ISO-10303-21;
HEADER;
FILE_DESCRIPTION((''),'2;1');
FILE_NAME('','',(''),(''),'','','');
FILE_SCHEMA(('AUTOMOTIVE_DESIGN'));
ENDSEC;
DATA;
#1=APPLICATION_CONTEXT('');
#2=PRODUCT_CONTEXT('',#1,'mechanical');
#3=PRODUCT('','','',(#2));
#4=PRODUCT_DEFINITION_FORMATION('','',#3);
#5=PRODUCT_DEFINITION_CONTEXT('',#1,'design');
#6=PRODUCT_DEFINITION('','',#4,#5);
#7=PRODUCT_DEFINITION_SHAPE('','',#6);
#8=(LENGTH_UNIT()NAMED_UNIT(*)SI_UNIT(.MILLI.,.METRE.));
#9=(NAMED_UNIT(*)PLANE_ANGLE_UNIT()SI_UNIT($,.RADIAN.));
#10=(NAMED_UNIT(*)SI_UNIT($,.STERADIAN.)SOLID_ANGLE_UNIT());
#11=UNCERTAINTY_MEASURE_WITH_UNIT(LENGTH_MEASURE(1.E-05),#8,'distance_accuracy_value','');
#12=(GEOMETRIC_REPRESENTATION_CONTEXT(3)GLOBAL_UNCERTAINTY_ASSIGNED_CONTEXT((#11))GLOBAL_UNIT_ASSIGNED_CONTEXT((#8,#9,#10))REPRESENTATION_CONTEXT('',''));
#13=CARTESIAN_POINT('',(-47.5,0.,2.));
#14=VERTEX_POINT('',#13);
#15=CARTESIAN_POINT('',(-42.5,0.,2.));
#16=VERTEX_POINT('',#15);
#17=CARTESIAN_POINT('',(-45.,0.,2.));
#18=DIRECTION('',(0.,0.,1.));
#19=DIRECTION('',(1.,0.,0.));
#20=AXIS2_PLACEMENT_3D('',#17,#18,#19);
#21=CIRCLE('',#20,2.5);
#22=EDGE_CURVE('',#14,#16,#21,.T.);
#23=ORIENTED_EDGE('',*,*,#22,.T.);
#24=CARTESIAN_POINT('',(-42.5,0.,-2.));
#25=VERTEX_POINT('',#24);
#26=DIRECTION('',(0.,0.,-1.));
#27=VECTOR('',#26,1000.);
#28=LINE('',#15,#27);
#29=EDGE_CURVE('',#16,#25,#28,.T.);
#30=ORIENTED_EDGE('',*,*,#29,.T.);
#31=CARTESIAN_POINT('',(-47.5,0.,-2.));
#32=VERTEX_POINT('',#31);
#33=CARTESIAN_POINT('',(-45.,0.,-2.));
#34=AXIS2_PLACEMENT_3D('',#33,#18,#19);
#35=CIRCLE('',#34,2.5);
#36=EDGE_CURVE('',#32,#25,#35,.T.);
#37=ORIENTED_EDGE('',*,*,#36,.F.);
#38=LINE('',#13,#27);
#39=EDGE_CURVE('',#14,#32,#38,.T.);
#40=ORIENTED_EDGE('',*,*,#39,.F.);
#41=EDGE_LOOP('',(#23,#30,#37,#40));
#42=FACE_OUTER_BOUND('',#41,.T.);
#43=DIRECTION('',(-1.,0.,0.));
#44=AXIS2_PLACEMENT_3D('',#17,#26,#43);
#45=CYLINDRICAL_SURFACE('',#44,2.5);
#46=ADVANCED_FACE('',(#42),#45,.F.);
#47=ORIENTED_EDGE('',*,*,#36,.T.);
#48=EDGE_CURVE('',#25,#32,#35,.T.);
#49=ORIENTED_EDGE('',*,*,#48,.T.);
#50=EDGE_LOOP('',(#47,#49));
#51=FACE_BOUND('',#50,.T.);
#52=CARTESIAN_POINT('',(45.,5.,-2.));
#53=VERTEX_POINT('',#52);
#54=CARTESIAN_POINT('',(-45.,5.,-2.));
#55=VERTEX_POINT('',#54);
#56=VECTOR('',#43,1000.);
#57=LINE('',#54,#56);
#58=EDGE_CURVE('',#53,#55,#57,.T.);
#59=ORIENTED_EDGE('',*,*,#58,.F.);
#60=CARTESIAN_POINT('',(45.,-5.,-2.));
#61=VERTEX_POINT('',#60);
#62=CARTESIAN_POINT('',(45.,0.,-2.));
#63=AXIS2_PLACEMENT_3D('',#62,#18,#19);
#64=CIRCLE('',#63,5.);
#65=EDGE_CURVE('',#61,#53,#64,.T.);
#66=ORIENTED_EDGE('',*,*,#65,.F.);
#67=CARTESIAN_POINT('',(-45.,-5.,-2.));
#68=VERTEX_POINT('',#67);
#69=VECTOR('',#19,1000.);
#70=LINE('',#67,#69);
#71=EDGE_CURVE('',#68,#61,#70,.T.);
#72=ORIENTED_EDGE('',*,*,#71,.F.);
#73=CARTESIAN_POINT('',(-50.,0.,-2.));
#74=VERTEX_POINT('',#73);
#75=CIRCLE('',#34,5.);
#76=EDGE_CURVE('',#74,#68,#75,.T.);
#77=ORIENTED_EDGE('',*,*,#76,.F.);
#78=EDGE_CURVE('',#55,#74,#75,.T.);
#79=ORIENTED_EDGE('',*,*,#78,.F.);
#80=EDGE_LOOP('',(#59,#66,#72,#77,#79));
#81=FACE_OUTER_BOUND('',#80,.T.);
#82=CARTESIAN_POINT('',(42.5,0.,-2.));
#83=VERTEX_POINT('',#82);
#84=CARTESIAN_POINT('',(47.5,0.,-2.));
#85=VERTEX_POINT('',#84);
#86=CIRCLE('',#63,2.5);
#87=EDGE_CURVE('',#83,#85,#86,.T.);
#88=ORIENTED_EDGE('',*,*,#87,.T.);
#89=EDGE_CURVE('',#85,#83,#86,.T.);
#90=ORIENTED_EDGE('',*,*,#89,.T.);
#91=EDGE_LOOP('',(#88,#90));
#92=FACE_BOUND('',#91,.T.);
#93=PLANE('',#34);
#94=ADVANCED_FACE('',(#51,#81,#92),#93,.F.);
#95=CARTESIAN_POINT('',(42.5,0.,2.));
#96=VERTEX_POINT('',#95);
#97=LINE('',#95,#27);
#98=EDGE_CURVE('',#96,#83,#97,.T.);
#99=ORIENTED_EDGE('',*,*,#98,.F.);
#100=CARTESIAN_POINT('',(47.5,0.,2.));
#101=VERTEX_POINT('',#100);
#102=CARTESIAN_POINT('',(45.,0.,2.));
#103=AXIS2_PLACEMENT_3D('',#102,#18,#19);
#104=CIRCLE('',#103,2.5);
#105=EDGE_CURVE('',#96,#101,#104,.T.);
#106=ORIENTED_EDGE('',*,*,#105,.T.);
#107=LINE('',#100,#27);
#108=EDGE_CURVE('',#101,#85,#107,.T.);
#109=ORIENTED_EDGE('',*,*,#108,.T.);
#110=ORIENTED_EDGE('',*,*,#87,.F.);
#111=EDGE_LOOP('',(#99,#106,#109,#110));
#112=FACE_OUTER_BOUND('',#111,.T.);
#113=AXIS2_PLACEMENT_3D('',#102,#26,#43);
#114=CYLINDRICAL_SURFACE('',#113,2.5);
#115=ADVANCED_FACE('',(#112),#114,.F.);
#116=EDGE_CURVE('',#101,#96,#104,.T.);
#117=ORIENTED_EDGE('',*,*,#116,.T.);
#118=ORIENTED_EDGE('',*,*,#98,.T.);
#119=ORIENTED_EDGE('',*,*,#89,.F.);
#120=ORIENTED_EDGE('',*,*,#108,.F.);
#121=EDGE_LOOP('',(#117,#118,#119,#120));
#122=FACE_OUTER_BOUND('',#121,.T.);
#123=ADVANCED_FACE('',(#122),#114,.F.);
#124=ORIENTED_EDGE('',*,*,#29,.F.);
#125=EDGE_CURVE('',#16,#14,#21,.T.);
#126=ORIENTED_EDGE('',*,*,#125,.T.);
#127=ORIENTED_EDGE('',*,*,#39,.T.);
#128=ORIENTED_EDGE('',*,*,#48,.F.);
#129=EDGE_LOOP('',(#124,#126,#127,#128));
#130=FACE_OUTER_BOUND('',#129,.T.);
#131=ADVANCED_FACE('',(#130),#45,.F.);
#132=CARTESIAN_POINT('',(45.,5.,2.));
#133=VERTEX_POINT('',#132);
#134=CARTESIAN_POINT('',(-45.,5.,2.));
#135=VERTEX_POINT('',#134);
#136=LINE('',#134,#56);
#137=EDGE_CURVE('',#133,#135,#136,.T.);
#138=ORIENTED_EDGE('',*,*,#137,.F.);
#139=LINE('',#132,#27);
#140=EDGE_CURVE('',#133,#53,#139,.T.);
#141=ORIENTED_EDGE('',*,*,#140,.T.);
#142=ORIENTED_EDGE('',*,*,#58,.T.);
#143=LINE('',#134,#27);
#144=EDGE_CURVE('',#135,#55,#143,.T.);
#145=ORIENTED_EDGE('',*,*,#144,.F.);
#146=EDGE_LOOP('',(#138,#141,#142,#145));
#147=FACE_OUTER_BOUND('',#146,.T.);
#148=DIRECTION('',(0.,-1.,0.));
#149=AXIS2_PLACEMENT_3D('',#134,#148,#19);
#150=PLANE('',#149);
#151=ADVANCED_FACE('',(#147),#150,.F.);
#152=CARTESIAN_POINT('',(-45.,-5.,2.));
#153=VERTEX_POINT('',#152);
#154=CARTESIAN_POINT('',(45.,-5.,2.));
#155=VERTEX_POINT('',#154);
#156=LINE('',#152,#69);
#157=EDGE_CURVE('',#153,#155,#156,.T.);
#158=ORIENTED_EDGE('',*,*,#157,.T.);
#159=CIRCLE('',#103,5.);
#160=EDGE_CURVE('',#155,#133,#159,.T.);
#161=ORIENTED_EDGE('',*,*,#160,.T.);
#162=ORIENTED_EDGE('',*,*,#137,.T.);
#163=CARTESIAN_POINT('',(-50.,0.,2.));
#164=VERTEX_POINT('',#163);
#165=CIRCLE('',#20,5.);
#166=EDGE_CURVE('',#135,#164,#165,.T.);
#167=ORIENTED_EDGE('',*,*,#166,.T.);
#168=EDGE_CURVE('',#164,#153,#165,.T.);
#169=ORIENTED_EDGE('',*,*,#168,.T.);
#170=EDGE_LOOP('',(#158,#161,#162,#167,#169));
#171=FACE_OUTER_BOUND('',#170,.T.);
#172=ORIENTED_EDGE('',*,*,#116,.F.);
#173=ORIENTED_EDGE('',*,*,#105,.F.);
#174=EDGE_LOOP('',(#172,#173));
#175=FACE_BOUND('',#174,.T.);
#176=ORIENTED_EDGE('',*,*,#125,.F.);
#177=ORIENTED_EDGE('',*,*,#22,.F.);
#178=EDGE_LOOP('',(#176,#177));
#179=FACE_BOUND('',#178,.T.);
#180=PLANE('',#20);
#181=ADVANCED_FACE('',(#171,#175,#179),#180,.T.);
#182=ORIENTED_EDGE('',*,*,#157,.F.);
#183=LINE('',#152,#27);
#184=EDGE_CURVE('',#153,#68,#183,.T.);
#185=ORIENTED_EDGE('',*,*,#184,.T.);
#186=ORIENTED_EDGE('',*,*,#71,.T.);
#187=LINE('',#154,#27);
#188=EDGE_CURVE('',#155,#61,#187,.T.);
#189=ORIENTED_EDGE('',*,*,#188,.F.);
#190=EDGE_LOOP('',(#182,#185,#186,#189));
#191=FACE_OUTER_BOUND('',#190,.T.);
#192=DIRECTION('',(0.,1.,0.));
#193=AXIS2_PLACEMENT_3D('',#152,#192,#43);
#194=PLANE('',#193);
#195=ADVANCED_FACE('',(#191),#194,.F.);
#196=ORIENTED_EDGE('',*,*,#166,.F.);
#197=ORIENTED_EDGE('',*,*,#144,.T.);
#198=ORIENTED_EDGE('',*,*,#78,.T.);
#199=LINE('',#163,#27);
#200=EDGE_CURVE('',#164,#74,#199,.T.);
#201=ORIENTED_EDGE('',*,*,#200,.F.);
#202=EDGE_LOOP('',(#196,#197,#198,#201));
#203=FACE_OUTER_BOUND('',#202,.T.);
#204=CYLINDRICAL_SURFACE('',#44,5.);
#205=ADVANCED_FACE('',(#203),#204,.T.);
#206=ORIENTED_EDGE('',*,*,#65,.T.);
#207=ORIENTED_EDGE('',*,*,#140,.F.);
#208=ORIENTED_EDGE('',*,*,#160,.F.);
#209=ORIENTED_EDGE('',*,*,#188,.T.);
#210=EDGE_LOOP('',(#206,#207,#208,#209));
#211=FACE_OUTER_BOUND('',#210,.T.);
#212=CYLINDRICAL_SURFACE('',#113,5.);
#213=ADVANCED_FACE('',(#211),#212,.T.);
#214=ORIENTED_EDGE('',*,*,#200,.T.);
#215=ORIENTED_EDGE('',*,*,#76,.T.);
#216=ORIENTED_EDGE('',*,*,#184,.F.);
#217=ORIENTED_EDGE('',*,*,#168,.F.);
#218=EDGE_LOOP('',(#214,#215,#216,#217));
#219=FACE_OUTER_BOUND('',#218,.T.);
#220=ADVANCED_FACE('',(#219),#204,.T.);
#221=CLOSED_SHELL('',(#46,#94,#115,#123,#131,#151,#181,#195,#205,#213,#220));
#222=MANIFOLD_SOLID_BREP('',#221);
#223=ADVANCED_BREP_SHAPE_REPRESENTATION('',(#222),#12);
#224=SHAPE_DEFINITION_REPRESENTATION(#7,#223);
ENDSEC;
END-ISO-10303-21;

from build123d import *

# Parameters (mm, degrees)
LINK_PROFILE_SKETCH_R = 2.5
LINK_BAR_4MM_DEPTH    = 2


with BuildPart() as part:
    # Link Profile Sketch → Link Bar 4mm (new, symmetric)
    with BuildSketch(Plane.XY):
        with BuildLine():
            Line((-45, 5), (45, 5))
            ThreePointArc((45, 5), (50, 0), (45, -5))
            Line((45, -5), (-45, -5))
            ThreePointArc((-45, -5), (-50, 0), (-45, 5))
        make_face()
        with Locations((-45, 0)):
            Circle(LINK_PROFILE_SKETCH_R, mode=Mode.SUBTRACT)
        with Locations((45, 0)):
            Circle(LINK_PROFILE_SKETCH_R, mode=Mode.SUBTRACT)
    extrude(amount=LINK_BAR_4MM_DEPTH, both=True)


solid = part.part
